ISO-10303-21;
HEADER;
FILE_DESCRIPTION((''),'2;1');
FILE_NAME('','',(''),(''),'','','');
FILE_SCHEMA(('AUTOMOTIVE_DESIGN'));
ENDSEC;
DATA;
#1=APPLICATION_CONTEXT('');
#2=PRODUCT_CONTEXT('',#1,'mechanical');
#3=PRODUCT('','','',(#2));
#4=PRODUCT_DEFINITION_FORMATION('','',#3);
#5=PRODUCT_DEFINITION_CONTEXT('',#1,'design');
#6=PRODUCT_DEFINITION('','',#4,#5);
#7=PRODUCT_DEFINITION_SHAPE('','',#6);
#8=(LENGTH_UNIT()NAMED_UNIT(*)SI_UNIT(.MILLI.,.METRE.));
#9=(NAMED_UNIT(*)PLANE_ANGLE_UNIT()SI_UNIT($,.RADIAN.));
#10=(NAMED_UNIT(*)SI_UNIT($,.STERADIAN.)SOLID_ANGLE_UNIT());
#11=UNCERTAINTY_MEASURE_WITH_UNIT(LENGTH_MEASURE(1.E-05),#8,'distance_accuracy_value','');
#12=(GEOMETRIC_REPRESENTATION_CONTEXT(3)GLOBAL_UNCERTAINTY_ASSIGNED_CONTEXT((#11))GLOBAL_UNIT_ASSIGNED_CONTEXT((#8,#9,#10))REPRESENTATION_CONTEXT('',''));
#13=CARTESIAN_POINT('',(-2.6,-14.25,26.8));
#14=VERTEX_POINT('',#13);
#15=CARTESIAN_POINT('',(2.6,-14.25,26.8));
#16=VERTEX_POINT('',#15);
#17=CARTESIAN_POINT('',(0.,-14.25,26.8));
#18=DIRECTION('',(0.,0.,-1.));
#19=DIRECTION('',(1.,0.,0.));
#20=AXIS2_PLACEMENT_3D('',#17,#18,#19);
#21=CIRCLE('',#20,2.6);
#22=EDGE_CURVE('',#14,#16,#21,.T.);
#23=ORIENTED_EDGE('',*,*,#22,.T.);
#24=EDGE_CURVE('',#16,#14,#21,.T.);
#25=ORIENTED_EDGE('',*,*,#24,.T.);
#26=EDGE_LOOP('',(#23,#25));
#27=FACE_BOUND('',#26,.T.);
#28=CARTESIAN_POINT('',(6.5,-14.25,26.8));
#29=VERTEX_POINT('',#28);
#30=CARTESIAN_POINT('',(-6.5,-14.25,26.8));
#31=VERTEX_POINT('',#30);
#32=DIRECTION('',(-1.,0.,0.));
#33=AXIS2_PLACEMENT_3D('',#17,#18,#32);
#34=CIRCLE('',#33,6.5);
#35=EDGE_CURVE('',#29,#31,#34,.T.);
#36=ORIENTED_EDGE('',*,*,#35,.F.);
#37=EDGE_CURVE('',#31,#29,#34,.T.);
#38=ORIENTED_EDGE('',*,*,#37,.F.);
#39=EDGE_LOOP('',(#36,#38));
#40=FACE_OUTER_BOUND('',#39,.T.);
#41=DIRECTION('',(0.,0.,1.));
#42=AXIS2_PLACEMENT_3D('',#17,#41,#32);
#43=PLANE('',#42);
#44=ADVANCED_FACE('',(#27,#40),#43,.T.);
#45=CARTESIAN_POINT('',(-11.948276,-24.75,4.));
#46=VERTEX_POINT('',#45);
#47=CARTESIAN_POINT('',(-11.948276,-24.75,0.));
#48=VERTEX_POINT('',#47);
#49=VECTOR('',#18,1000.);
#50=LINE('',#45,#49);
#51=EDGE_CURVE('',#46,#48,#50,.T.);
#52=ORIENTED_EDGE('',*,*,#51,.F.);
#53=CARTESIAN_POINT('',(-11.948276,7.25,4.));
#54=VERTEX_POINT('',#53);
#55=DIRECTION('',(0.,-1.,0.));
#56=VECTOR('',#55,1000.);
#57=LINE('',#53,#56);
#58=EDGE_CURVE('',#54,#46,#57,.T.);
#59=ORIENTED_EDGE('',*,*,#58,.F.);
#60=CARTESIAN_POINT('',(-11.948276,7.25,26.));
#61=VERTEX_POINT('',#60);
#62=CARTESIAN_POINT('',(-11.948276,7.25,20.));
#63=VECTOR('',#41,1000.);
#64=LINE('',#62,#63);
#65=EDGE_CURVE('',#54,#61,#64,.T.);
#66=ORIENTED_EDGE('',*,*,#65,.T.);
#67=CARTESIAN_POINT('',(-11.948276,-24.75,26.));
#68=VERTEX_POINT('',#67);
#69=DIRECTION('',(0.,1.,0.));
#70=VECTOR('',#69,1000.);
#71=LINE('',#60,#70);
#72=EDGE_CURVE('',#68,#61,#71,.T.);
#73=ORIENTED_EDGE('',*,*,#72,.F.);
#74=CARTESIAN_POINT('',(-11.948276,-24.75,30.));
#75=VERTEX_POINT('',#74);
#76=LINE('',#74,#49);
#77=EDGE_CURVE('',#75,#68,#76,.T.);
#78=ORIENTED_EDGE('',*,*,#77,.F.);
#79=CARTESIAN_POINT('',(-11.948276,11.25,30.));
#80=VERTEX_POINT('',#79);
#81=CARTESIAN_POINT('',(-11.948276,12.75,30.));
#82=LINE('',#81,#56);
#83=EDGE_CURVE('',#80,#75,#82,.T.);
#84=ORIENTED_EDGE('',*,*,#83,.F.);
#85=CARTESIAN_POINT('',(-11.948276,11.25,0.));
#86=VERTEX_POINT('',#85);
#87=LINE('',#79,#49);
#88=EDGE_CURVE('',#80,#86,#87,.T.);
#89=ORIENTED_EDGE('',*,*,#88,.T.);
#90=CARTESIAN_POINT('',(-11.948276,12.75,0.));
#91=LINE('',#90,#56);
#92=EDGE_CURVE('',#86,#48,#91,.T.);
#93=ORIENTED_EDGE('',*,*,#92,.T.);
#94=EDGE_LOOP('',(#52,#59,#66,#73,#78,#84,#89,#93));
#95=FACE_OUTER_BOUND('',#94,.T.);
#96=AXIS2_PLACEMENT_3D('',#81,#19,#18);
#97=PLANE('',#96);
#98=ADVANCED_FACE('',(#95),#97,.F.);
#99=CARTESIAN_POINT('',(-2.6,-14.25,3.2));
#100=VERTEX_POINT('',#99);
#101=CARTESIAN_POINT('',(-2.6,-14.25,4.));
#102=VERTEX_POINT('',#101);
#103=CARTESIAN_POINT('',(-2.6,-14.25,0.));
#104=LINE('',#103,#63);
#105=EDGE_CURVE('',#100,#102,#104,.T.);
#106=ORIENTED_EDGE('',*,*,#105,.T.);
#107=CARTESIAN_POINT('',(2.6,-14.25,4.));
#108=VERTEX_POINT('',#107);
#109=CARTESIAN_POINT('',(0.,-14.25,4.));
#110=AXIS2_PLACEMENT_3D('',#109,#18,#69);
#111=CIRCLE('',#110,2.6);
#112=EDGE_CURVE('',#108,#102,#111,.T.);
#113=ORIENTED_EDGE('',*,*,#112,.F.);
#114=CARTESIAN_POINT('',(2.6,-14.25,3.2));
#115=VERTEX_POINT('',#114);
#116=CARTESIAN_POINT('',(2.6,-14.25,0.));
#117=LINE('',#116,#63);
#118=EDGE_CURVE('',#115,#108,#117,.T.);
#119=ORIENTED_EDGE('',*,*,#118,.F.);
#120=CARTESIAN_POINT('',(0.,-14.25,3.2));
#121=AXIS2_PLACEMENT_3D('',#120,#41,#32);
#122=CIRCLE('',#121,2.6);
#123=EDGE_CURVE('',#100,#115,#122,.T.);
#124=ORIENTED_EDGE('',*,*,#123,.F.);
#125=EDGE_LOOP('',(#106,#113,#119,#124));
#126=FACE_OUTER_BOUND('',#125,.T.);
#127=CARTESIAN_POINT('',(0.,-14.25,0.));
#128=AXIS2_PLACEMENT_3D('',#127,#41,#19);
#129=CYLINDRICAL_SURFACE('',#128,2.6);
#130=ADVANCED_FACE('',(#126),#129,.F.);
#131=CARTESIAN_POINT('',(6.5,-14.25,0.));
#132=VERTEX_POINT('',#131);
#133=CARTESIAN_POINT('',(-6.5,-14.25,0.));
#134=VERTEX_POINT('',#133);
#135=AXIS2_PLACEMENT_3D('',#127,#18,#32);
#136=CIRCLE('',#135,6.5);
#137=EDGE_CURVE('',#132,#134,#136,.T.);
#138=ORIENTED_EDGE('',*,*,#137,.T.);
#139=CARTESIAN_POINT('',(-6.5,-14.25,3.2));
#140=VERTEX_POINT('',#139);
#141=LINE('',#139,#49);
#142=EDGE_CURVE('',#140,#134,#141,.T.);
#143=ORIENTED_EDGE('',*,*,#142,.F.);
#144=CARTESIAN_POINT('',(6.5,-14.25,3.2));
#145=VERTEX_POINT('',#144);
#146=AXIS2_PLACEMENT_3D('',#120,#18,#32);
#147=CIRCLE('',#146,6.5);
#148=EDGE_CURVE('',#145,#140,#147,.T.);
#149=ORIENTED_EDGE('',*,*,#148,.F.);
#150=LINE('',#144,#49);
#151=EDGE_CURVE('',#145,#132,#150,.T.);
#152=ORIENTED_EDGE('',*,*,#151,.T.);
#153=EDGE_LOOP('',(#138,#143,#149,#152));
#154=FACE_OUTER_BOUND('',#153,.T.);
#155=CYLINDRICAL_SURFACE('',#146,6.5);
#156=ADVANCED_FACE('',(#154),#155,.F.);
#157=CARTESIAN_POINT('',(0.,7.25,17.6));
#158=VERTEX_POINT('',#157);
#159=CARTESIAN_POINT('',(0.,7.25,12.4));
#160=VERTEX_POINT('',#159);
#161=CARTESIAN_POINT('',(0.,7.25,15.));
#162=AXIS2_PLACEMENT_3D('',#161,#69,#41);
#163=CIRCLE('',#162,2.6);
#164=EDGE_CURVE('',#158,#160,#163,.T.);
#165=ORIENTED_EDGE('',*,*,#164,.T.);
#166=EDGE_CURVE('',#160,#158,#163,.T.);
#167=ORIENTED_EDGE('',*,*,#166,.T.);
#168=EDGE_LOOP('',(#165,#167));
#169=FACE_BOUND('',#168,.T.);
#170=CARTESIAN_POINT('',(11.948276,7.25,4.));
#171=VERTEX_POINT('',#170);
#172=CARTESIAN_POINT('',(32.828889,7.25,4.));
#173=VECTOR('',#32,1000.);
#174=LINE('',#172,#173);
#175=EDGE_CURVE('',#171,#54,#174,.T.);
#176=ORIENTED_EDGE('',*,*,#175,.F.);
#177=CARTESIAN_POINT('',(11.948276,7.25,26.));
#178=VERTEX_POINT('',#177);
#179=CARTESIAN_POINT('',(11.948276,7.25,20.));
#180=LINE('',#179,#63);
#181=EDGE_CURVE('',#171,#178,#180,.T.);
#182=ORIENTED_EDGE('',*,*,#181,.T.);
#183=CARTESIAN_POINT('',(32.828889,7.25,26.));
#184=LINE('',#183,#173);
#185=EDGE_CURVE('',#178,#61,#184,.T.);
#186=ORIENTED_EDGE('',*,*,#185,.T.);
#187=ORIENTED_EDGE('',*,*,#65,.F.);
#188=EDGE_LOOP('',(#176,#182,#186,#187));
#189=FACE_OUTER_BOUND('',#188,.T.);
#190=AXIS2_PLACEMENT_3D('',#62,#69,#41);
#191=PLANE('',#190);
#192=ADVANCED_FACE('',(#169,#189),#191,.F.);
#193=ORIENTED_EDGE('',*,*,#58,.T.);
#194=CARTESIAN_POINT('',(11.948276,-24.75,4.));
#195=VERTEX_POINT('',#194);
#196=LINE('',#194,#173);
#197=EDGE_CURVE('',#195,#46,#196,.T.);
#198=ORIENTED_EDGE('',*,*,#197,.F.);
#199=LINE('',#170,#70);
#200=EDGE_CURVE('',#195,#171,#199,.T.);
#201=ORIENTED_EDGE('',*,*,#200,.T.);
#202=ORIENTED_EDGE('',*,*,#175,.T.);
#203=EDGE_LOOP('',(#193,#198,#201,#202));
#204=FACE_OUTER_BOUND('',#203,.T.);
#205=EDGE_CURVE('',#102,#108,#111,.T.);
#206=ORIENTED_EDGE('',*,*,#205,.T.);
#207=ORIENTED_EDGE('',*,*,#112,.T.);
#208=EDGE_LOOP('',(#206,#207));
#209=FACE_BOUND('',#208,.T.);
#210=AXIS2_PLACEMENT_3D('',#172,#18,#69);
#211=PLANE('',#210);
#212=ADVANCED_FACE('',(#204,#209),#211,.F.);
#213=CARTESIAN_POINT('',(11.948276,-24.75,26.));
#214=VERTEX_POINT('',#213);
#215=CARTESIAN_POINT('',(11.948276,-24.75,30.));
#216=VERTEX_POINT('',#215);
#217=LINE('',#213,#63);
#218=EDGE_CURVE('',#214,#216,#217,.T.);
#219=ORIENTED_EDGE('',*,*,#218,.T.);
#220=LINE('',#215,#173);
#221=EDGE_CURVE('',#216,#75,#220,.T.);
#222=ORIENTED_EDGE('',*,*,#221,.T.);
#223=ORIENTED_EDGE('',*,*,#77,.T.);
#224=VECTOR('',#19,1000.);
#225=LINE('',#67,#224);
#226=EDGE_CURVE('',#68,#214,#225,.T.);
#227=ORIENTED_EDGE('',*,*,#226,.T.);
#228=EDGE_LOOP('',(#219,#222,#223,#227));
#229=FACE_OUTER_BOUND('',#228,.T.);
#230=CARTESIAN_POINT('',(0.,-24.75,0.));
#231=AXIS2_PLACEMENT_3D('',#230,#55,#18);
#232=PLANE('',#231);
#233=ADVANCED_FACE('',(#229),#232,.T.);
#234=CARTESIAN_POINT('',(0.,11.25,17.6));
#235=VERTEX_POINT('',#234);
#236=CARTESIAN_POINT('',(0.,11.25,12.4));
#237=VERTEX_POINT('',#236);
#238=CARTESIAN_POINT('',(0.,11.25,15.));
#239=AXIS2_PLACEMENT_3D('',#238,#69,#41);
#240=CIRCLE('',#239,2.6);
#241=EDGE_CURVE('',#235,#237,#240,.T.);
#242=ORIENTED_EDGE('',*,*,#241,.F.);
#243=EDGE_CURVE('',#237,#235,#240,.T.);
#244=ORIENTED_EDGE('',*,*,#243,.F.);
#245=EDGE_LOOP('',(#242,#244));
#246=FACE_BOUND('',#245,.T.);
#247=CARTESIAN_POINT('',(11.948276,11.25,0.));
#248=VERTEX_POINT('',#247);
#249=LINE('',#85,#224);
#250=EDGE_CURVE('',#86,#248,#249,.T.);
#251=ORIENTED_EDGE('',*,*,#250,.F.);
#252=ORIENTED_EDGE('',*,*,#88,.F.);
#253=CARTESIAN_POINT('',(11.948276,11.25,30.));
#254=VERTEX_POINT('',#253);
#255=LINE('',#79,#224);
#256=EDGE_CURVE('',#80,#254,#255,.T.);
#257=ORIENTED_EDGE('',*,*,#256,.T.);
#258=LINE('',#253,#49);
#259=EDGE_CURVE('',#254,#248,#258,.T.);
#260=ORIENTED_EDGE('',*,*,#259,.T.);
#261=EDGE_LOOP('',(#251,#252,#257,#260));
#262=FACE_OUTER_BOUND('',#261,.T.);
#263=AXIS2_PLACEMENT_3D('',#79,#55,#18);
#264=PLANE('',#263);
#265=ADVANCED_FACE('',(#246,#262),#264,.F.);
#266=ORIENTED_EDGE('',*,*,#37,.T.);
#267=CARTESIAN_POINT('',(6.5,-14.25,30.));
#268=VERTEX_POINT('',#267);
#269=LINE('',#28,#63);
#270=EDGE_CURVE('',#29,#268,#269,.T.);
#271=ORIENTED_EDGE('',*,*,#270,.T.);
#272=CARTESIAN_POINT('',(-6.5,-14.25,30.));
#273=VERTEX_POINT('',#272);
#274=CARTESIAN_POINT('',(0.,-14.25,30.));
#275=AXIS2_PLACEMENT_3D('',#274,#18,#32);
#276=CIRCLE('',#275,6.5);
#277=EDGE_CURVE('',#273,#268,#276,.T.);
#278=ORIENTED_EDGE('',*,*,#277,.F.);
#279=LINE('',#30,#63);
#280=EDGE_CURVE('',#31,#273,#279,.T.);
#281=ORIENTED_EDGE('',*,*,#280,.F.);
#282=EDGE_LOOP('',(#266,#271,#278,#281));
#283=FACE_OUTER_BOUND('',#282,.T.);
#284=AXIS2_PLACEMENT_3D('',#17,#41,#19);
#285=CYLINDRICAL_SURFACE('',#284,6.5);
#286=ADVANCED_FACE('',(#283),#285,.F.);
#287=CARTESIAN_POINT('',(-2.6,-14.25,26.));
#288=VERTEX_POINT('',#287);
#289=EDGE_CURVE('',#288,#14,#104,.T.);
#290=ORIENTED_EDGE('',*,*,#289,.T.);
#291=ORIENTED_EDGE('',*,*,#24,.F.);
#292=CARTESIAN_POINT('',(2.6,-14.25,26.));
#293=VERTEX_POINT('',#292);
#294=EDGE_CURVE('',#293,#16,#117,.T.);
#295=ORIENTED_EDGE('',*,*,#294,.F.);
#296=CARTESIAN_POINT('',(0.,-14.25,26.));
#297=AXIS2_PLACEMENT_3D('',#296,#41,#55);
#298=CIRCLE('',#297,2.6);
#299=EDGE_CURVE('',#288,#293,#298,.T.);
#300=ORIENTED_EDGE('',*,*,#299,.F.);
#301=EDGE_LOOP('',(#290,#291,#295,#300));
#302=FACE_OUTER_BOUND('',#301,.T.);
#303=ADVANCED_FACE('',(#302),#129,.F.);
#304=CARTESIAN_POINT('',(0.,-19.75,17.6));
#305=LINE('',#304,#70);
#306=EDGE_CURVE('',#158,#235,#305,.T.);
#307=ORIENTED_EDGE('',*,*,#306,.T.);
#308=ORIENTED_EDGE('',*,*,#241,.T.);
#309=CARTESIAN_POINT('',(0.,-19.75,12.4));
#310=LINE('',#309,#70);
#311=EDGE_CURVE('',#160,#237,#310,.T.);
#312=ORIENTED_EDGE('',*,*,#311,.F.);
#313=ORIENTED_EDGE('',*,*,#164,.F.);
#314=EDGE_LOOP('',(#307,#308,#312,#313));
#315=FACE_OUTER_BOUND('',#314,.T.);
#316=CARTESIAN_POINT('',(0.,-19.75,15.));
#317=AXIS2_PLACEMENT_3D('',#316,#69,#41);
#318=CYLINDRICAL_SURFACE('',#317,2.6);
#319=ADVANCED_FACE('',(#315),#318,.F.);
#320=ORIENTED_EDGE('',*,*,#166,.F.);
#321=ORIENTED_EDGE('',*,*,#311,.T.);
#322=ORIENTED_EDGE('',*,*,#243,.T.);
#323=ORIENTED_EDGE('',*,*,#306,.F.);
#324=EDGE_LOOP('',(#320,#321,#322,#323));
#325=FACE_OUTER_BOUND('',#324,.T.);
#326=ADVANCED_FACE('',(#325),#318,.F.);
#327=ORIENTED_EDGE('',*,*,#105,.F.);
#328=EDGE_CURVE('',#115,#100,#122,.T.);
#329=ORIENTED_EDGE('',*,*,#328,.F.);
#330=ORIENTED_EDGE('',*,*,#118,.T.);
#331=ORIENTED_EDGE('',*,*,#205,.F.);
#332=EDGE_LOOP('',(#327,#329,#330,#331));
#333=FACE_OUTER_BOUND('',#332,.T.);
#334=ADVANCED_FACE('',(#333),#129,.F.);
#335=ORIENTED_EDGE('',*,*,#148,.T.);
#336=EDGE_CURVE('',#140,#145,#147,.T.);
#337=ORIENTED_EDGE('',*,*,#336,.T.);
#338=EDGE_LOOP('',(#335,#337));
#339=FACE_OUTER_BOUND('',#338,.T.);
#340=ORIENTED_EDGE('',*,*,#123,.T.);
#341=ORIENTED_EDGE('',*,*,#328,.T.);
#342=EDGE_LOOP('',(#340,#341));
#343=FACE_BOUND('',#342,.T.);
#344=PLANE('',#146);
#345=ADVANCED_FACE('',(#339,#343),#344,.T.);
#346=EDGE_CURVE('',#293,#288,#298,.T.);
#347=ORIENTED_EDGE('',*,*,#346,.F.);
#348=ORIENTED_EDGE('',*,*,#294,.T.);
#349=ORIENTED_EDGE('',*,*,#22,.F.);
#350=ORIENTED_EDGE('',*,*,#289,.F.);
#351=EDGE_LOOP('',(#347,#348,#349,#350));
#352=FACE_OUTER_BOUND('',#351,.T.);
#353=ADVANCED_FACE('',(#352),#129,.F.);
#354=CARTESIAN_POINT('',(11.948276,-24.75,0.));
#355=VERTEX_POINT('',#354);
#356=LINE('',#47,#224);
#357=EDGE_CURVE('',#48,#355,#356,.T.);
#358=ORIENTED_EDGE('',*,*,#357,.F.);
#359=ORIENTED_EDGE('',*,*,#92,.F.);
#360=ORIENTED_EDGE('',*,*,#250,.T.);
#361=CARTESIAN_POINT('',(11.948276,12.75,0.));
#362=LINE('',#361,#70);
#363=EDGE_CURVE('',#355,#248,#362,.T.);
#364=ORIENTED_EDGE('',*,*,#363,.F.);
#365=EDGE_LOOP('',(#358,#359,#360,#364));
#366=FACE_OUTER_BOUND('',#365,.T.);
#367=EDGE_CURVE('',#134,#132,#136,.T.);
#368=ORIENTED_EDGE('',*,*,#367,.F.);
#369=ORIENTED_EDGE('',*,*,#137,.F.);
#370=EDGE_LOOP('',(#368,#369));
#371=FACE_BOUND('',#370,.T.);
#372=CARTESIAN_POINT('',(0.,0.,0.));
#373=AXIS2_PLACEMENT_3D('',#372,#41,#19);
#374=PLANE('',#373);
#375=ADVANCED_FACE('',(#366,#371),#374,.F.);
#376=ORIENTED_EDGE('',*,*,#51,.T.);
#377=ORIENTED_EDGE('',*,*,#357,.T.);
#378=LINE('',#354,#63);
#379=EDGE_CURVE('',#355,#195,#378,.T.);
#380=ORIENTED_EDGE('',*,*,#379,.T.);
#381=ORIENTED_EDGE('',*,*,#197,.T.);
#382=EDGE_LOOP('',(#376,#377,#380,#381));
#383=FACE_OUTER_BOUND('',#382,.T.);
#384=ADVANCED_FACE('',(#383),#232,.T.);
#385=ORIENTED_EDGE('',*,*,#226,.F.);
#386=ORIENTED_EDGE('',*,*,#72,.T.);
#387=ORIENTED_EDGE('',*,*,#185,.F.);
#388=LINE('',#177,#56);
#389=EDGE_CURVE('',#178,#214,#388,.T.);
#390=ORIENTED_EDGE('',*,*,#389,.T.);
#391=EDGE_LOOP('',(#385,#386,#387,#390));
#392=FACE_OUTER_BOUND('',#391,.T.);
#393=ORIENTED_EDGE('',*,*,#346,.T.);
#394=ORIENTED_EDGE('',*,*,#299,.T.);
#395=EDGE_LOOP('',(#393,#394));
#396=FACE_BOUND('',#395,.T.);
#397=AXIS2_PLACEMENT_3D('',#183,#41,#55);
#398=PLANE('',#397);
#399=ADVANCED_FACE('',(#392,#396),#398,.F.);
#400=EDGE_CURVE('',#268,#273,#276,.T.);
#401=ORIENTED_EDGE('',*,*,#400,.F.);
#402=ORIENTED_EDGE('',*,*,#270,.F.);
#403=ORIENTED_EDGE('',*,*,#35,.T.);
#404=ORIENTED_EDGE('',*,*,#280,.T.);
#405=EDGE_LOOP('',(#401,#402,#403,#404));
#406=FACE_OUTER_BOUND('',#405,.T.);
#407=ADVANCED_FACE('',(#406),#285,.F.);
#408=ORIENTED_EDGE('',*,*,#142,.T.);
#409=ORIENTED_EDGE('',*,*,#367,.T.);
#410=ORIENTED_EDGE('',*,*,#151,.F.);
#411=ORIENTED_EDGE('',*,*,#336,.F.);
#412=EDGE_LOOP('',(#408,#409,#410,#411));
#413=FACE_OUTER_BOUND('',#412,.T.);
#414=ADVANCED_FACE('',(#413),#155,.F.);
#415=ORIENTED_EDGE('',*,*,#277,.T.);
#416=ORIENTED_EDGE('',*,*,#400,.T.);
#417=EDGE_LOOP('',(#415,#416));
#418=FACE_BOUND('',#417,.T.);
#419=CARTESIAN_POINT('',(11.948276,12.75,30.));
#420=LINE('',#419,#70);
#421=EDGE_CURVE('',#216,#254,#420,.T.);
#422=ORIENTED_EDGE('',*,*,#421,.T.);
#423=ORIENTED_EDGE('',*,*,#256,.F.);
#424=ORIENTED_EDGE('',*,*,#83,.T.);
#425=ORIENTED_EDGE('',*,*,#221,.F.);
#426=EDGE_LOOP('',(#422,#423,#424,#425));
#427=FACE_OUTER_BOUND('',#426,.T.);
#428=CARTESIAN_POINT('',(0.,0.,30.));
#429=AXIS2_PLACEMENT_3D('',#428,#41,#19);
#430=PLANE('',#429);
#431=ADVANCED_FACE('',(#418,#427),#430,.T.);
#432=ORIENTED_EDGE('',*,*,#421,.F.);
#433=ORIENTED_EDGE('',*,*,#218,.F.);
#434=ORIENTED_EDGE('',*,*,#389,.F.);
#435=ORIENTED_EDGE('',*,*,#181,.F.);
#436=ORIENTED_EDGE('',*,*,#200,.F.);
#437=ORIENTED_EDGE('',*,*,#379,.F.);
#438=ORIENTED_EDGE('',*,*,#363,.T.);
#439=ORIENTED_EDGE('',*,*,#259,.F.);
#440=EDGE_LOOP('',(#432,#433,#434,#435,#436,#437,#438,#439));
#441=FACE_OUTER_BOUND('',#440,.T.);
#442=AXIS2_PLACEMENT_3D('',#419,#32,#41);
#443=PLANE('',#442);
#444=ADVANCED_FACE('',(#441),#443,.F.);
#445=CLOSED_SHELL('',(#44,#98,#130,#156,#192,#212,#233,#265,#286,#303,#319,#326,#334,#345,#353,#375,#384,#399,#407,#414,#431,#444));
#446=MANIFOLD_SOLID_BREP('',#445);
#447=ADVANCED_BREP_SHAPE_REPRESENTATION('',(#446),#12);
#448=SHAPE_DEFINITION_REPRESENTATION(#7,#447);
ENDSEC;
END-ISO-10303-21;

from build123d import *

# Parameters (mm, degrees)
SKETCH1_W           = 23.896551724
SKETCH1_H           = 25.5
BOSS_EXTRUDE1_DEPTH = 30
CUT_EXTRUDE1_DEPTH  = 41.417912914
SKETCH4_W           = 10
SKETCH4_H           = 5
CUT_EXTRUDE3_DEPTH  = 41.417912914
SKETCH7_W           = 6
SKETCH7_H           = 20
CUT_EXTRUDE4_DEPTH  = 23.896551724
SKETCH9_W           = 23.896551724
SKETCH9_H           = 30
BOSS_EXTRUDE3_DEPTH = 17.5
SKETCH12_W          = 23.896551724
SKETCH12_H          = 30
CUT_EXTRUDE7_DEPTH  = 8
SKETCH15_W          = 23.896551724
SKETCH15_H          = 30
CUT_EXTRUDE11_DEPTH = 6
SKETCH18_W          = 23.896551724
SKETCH18_H          = 4
BOSS_EXTRUDE4_DEPTH = 7
SKETCH19_W          = 30
SKETCH19_H          = 5
CUT_EXTRUDE12_DEPTH = 44.140557302
SKETCH20_R          = 2.6
CUT_EXTRUDE13_DEPTH = 45.763392366
SKETCH21_W          = 23.896551724
SKETCH21_H          = 4
BOSS_EXTRUDE5_DEPTH = 5
SKETCH22_R          = 2.6
CUT_EXTRUDE14_DEPTH = 41.685670648
SKETCH23_R          = 6.5
CUT_EXTRUDE15_DEPTH = 3.2


with BuildPart() as part:
    # Sketch1 → Boss-Extrude1 (new body)
    with BuildSketch(Plane.XY):
        Rectangle(SKETCH1_W, SKETCH1_H)
    extrude(amount=BOSS_EXTRUDE1_DEPTH)

    # Sketch2 → Cut-Extrude1 (cut, through all)
    with BuildSketch(Plane(origin=(11.948275862, 0, 0), x_dir=(0, 0, -1), z_dir=(1, 0, 0))):
        Polygon((-15, -12.75), (-20, -12.75), (-20, 2.25), (-10, 2.25), (-10, -12.75), align=None)
    extrude(amount=-CUT_EXTRUDE1_DEPTH, mode=Mode.SUBTRACT)

    # Sketch4 → Cut-Extrude3 (cut, through all)
    with BuildSketch(Plane(origin=(11.948275862, 0, 0), x_dir=(0, 0, -1), z_dir=(1, 0, 0))):
        with Locations((-15, 4.75)):
            Rectangle(SKETCH4_W, SKETCH4_H)
    extrude(amount=-CUT_EXTRUDE3_DEPTH, mode=Mode.SUBTRACT)

    # Sketch7 → Cut-Extrude4 (cut)
    with BuildSketch(Plane.ZY.offset(11.948275862)):
        with Locations((7, -2.75)):
            Rectangle(SKETCH7_W, SKETCH7_H)
        with Locations((23, -2.75)):
            Rectangle(SKETCH7_W, SKETCH7_H)
    extrude(amount=-CUT_EXTRUDE4_DEPTH, mode=Mode.SUBTRACT)

    # Sketch9 → Boss-Extrude3 (add)
    with BuildSketch(Plane(origin=(0, 12.75, 0), x_dir=(1, 0, 0), z_dir=(0, 1, 0))):
        with Locations((0, -15)):
            Rectangle(SKETCH9_W, SKETCH9_H)
    extrude(amount=BOSS_EXTRUDE3_DEPTH)

    # Sketch12 → Cut-Extrude7 (cut)
    with BuildSketch(Plane(origin=(0, 30.25, 0), x_dir=(1, 0, 0), z_dir=(0, 1, 0))):
        with Locations((0, -15)):
            Rectangle(SKETCH12_W, SKETCH12_H)
    extrude(amount=-CUT_EXTRUDE7_DEPTH, mode=Mode.SUBTRACT)

    # Sketch15 → Cut-Extrude11 (cut)
    with BuildSketch(Plane(origin=(0, 22.25, 0), x_dir=(1, 0, 0), z_dir=(0, 1, 0))):
        with Locations((0, -15)):
            Rectangle(SKETCH15_W, SKETCH15_H)
    extrude(amount=-CUT_EXTRUDE11_DEPTH, mode=Mode.SUBTRACT)

    # Sketch18 → Boss-Extrude4 (add)
    with BuildSketch(Plane.XZ.offset(12.75)):
        with Locations((0, 28)):
            Rectangle(SKETCH18_W, SKETCH18_H)
        with Locations((0, 2)):
            Rectangle(SKETCH18_W, SKETCH18_H)
    extrude(amount=BOSS_EXTRUDE4_DEPTH)

    # Sketch19 → Cut-Extrude12 (cut, through all)
    with BuildSketch(Plane(origin=(11.948275862, 0, 0), x_dir=(0, 0, -1), z_dir=(1, 0, 0))):
        with Locations((-15, 13.75)):
            Rectangle(SKETCH19_W, SKETCH19_H)
    extrude(amount=-CUT_EXTRUDE12_DEPTH, mode=Mode.SUBTRACT)

    # Sketch20 → Cut-Extrude13 (cut, through all)
    with BuildSketch(Plane(origin=(0, 11.25, 0), x_dir=(1, 0, 0), z_dir=(0, 1, 0))):
        with Locations(Location((0, -15, 0), (0, 0, 270))):
            Circle(SKETCH20_R)
    extrude(amount=-CUT_EXTRUDE13_DEPTH, mode=Mode.SUBTRACT)

    # Sketch21 → Boss-Extrude5 (add)
    with BuildSketch(Plane.XZ.offset(19.75)):
        with Locations((0, 2)):
            Rectangle(SKETCH21_W, SKETCH21_H)
        with Locations((0, 28)):
            Rectangle(SKETCH21_W, SKETCH21_H)
    extrude(amount=BOSS_EXTRUDE5_DEPTH)

    # Sketch22 → Cut-Extrude14 (cut, through all)
    with BuildSketch(Plane.XY.offset(30)):
        with Locations((0, -14.25)):
            Circle(SKETCH22_R)
    extrude(amount=-CUT_EXTRUDE14_DEPTH, mode=Mode.SUBTRACT)

    # Sketch23 → Cut-Extrude15 (cut)
    with BuildSketch(Plane(origin=(0, 0, 0), x_dir=(-1, 0, 0), z_dir=(0, 0, -1))):
        with Locations((0, -14.25)):
            Circle(SKETCH23_R)
    cut_extrude15 = extrude(amount=-CUT_EXTRUDE15_DEPTH, mode=Mode.SUBTRACT)

    # Mirror1: Cut-Extrude15 across plane
    add(cut_extrude15.mirror(Plane(origin=(0, 0, 15), x_dir=(1, 0, 0), z_dir=(0, 0, -1))), mode=Mode.SUBTRACT)


solid = part.part
